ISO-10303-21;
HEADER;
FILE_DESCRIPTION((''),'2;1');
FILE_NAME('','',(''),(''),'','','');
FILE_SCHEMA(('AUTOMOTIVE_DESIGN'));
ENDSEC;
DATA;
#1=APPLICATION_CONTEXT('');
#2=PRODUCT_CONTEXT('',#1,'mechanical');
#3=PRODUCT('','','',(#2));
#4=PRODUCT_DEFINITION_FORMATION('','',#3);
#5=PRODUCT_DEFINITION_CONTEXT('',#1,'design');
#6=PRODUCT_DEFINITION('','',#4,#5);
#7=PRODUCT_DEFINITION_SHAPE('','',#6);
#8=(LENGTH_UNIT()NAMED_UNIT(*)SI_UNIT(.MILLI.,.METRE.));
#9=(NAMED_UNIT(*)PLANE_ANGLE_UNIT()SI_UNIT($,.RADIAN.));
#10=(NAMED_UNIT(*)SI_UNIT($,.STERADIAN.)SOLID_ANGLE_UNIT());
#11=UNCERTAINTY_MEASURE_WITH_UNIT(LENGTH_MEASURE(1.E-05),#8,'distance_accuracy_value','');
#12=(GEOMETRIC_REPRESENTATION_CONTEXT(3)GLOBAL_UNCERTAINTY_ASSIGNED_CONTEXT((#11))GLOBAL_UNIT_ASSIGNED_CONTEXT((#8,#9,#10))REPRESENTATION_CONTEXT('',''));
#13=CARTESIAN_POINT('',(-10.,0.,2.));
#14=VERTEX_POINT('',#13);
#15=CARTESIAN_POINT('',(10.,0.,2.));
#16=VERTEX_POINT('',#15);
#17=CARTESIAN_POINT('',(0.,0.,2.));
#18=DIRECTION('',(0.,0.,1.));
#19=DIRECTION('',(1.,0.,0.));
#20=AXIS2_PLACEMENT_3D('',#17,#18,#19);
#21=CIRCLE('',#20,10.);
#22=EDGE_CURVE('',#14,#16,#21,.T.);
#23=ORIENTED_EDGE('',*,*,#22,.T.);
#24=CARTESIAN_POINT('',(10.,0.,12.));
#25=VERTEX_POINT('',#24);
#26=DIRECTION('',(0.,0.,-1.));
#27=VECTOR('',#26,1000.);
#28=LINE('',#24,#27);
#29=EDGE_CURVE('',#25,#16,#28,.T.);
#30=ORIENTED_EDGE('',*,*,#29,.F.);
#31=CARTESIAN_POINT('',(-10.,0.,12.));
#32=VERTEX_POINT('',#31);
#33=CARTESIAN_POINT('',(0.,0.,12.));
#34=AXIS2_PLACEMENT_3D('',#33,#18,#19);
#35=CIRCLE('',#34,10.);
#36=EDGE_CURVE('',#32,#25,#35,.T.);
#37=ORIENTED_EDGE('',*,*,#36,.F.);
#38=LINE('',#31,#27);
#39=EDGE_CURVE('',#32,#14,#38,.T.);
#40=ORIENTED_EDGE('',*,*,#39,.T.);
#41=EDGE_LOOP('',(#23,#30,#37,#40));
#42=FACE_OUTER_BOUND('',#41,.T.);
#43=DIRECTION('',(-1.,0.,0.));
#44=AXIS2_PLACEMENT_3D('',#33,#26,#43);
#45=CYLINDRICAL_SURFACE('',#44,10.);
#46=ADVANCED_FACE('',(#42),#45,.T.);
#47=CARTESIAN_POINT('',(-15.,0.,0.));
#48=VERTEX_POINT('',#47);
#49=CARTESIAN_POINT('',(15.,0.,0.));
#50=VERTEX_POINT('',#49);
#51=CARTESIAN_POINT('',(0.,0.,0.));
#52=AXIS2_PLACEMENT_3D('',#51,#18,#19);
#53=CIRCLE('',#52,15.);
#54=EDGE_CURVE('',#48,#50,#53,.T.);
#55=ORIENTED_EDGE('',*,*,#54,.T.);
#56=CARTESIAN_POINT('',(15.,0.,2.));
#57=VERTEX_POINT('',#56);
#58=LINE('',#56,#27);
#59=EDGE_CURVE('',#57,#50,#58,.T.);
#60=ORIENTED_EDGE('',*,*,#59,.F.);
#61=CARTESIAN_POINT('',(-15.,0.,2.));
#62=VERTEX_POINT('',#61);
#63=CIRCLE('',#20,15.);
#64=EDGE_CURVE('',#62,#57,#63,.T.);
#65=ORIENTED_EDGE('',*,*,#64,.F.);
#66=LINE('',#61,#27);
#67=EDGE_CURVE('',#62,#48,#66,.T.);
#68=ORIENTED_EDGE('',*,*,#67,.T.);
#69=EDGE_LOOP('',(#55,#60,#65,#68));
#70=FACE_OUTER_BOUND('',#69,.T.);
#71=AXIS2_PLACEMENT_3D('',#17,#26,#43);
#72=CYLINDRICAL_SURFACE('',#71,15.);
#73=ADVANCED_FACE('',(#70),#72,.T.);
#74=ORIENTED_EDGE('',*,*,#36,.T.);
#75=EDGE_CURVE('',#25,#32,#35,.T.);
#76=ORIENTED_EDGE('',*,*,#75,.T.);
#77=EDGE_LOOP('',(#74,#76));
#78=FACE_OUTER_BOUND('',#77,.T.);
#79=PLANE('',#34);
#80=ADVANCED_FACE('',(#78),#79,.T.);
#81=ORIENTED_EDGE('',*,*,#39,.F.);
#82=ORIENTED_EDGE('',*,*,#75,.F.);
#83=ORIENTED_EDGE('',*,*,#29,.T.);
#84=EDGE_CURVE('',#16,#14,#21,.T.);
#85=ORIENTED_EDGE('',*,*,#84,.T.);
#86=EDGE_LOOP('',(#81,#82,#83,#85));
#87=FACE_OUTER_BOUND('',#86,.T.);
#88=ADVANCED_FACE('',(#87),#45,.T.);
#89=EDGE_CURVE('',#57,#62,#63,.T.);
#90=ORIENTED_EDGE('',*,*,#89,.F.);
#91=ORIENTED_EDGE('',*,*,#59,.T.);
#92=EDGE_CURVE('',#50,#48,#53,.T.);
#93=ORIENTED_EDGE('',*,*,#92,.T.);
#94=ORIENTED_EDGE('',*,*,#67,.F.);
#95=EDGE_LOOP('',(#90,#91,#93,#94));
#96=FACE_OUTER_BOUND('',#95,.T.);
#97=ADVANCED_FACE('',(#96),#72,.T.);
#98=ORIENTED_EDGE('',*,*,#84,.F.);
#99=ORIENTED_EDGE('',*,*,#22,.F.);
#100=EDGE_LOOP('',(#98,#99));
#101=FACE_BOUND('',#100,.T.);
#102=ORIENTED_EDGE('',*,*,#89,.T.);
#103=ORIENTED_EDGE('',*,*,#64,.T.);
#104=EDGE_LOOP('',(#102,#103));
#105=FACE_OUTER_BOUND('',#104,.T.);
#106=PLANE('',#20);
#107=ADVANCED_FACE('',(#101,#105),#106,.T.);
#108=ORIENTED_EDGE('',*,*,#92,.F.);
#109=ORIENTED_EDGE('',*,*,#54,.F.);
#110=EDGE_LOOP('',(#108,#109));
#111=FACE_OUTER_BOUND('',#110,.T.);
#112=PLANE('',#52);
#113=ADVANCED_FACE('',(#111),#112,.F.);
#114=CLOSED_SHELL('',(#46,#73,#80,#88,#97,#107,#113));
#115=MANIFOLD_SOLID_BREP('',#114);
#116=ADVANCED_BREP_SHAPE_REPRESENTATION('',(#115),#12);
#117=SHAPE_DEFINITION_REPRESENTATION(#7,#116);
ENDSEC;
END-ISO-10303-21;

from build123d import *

# Parameters (mm, degrees)
SKETCH1_R           = 15
BOSS_EXTRUDE1_DEPTH = 2
SKETCH2_R           = 10
BOSS_EXTRUDE2_DEPTH = 10


with BuildPart() as part:
    # Sketch1 → Boss-Extrude1 (new body)
    with BuildSketch(Plane.XY):
        Circle(SKETCH1_R)
    extrude(amount=BOSS_EXTRUDE1_DEPTH)

    # Sketch2 → Boss-Extrude2 (add)
    with BuildSketch(Plane.XY.offset(2)):
        Circle(SKETCH2_R)
    extrude(amount=BOSS_EXTRUDE2_DEPTH)


solid = part.part
